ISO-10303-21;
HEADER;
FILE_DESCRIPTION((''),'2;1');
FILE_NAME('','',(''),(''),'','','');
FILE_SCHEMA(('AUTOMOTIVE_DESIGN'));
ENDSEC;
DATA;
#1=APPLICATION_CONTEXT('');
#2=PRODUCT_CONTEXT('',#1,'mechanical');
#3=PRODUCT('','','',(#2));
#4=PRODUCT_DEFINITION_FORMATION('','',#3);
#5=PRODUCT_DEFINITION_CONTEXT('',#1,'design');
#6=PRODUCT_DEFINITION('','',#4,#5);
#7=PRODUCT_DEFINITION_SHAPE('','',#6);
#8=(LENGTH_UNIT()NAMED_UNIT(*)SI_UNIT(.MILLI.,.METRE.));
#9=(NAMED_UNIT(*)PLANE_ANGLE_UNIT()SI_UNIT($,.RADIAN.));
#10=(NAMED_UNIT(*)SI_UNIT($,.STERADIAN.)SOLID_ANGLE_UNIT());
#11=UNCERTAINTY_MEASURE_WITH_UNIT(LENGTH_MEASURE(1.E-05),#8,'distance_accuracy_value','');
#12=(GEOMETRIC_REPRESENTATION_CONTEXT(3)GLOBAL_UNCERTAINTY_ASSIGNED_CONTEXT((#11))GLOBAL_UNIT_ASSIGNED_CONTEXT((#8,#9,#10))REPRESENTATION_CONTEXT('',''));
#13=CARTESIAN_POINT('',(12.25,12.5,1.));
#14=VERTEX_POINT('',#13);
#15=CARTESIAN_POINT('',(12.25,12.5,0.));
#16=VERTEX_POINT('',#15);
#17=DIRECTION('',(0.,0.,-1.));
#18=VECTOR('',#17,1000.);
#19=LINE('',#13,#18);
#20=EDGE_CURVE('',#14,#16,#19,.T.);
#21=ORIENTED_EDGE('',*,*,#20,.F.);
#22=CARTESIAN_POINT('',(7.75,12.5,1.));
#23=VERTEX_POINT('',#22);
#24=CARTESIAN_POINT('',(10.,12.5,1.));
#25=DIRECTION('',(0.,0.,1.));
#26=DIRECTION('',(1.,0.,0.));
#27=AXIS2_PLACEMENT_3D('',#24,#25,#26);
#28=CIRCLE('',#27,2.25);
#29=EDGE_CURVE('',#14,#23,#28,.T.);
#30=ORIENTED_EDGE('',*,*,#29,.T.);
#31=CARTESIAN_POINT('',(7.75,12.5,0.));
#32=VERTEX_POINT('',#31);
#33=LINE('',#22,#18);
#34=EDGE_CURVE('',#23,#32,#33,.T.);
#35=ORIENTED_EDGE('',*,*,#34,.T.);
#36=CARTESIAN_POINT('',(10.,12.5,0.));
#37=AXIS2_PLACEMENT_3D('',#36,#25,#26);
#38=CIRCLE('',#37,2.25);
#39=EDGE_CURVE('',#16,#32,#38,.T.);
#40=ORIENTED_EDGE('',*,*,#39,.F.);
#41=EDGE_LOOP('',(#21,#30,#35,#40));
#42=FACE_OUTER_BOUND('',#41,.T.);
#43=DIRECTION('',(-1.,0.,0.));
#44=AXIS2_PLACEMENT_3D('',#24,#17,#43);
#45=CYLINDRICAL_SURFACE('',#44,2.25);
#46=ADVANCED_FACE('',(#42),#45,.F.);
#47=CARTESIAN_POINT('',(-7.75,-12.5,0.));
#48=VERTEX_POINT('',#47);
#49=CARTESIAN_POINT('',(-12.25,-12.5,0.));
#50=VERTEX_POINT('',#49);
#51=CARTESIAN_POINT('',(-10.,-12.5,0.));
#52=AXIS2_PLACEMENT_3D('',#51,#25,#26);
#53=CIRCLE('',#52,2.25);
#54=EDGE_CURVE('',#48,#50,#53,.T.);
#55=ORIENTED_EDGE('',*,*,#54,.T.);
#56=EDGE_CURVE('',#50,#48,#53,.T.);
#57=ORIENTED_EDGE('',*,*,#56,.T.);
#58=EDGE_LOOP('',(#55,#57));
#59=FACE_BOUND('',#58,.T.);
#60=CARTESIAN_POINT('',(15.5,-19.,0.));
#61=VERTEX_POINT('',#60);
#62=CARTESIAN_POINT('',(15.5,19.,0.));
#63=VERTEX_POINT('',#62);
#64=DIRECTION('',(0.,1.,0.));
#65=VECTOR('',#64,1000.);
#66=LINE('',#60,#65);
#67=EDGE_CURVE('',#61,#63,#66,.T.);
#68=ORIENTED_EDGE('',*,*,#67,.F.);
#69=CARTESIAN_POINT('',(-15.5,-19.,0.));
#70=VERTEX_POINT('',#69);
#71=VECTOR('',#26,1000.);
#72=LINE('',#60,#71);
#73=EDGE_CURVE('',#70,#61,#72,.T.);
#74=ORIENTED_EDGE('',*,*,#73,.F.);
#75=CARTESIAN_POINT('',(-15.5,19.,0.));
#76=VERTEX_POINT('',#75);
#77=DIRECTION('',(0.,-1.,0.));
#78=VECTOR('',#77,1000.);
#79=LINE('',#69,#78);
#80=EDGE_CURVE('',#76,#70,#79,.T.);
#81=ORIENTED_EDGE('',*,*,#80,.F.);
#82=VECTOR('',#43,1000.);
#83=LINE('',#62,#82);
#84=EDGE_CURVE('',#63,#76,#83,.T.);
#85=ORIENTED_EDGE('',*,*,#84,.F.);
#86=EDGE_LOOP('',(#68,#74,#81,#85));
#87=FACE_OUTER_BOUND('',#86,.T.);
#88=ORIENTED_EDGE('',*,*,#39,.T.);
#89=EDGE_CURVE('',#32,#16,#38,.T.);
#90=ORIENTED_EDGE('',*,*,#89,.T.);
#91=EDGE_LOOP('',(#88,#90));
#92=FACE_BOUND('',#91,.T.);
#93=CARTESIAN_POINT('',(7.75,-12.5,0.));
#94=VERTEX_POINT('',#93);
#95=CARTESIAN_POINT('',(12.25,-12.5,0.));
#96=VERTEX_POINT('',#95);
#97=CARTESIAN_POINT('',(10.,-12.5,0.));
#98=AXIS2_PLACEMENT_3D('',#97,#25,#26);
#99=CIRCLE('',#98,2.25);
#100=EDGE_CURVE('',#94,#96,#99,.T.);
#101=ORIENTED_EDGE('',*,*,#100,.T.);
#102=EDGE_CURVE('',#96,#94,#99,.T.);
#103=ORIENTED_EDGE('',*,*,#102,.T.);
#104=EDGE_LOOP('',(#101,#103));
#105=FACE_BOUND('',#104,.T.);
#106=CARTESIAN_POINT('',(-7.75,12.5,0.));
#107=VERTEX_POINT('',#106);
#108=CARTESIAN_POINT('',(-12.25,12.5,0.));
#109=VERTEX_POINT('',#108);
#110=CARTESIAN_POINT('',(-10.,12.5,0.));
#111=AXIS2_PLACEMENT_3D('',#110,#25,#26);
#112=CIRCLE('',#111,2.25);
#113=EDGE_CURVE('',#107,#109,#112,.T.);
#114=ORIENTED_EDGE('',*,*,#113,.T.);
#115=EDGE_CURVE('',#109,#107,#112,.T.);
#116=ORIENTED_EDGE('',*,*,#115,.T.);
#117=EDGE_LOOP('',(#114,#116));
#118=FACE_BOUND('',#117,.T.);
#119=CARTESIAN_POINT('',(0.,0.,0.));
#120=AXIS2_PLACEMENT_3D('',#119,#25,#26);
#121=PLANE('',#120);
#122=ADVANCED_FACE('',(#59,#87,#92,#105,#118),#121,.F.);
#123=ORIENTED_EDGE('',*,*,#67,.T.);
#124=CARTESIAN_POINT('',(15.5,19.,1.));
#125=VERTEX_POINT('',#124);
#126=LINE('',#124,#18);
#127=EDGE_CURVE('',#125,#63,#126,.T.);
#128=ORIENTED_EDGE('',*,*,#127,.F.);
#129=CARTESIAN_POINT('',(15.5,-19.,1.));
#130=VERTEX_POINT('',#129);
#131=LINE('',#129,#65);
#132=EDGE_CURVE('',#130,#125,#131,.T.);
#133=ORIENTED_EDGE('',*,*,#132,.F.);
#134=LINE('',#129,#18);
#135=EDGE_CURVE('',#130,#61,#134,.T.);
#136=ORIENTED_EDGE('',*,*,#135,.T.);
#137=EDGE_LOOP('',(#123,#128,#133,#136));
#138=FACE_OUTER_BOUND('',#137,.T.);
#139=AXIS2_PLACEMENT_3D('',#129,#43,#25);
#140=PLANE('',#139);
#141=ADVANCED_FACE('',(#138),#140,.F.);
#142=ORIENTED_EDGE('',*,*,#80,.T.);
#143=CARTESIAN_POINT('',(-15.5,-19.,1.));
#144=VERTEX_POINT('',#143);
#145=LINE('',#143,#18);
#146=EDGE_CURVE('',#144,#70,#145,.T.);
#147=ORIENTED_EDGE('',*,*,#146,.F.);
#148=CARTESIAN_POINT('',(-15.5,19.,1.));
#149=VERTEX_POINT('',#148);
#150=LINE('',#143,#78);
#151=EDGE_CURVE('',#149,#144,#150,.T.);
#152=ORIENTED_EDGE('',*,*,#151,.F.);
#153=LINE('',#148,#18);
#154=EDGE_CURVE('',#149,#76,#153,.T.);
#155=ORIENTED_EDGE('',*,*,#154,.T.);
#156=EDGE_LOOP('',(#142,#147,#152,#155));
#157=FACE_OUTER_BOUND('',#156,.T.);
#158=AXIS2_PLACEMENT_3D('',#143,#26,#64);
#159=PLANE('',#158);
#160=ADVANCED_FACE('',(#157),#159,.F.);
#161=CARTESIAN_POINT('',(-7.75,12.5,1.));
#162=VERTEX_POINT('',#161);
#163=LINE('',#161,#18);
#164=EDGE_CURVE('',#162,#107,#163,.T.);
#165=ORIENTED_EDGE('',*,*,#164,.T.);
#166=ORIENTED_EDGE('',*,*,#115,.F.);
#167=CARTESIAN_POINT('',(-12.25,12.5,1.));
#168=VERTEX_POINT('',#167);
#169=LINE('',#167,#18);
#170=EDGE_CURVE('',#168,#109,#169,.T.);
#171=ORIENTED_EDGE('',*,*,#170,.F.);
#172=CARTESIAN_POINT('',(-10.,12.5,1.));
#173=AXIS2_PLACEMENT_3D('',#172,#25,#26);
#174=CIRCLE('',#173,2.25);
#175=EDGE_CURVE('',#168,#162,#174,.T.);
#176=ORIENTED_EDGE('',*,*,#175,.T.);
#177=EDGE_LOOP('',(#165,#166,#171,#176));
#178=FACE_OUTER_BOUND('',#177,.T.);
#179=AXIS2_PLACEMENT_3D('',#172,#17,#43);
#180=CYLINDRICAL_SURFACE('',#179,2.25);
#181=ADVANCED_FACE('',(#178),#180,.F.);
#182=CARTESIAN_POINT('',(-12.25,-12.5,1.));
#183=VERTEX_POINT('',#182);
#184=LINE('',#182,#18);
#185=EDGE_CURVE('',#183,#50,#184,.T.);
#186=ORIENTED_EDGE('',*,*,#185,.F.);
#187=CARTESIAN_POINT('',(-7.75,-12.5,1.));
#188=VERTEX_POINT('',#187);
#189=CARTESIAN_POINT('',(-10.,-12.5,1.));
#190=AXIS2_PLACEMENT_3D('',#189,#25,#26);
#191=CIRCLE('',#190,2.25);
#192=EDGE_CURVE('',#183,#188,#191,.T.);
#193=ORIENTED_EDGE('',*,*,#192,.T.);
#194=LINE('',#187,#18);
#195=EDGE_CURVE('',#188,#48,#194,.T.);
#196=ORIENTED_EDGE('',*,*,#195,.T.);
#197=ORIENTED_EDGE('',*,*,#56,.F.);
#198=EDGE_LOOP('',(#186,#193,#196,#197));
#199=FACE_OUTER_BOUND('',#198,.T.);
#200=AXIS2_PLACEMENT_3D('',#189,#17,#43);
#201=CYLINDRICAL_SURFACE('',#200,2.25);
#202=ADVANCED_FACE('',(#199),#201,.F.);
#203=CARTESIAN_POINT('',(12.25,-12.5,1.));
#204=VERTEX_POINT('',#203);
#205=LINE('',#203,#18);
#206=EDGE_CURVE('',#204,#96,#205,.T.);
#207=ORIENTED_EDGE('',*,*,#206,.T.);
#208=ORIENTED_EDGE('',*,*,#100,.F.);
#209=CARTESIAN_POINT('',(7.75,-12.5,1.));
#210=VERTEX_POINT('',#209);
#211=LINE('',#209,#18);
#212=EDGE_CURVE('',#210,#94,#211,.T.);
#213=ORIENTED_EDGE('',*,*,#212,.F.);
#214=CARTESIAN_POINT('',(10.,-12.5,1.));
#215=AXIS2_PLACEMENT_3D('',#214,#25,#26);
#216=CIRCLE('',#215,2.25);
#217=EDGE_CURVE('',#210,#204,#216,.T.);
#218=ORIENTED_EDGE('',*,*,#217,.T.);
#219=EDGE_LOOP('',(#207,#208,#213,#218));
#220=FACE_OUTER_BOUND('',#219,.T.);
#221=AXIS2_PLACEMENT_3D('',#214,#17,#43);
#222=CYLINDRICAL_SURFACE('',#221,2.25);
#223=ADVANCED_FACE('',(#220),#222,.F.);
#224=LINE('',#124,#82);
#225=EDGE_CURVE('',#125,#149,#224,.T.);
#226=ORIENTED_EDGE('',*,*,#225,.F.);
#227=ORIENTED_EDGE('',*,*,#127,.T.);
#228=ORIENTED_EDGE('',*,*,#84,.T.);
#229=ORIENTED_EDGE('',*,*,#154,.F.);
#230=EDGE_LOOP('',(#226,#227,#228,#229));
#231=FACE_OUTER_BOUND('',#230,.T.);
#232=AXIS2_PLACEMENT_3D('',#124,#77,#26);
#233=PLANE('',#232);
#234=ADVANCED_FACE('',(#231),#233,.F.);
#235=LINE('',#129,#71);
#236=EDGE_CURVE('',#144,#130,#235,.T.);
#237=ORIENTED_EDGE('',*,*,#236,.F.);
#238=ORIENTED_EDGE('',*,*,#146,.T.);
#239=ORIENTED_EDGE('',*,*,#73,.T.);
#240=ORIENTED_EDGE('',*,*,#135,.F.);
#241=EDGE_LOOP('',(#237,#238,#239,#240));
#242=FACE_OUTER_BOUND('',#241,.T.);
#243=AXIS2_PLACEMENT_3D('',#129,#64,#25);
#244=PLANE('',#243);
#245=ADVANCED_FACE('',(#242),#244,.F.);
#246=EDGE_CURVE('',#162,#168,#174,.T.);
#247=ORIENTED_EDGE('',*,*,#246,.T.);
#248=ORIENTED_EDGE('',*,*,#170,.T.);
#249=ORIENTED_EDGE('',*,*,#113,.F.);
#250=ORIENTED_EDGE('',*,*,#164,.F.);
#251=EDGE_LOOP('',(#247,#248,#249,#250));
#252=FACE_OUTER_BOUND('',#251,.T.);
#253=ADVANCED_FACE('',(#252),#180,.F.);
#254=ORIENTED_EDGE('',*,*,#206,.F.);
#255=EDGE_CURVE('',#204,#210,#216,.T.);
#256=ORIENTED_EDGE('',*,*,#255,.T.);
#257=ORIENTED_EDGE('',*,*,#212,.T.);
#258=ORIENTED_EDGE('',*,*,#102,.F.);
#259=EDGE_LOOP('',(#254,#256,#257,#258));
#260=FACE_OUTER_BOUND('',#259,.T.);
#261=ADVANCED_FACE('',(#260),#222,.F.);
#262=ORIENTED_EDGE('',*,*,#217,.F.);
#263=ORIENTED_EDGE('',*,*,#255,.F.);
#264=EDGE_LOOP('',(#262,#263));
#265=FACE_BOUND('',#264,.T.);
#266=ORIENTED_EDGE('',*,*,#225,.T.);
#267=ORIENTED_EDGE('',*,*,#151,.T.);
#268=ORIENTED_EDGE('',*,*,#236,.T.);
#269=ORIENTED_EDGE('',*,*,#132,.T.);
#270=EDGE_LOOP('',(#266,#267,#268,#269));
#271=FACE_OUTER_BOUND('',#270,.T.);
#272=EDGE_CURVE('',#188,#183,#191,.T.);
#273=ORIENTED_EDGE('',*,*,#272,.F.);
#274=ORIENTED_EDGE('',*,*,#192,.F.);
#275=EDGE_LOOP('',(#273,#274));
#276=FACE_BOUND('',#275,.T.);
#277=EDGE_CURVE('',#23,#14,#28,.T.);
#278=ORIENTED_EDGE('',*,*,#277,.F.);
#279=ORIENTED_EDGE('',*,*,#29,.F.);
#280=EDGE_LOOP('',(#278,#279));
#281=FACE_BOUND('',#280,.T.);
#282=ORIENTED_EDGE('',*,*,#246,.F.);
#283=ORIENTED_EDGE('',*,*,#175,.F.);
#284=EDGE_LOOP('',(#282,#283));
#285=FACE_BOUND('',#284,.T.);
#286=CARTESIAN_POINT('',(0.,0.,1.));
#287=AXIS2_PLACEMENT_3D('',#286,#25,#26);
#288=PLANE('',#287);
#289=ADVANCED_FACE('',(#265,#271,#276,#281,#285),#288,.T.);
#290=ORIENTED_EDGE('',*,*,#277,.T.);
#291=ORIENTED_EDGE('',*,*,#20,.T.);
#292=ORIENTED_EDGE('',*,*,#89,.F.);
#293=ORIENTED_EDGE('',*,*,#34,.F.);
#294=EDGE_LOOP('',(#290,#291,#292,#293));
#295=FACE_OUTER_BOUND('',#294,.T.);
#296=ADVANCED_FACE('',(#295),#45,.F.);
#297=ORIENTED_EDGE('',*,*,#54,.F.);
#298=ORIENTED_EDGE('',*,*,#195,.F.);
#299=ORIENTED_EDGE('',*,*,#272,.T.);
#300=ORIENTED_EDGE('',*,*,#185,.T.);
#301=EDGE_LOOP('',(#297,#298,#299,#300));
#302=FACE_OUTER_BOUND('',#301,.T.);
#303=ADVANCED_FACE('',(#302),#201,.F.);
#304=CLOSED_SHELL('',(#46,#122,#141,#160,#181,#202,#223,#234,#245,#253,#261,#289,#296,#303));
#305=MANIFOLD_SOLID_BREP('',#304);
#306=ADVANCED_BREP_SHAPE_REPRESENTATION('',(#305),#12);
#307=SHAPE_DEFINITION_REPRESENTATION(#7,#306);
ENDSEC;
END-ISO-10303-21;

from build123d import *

# Parameters (mm, degrees)
SKETCH_1_W      = 31
SKETCH_1_H      = 38
SKETCH_1_R      = 2.25
EXTRUDE_1_DEPTH = 1


with BuildPart() as part:
    # 草图1 → 凸台-拉伸1 (new body)
    with BuildSketch(Plane.XY):
        Rectangle(SKETCH_1_W, SKETCH_1_H)
        with Locations((-10, 12.5)):
            Circle(SKETCH_1_R, mode=Mode.SUBTRACT)
        with Locations((10, 12.5)):
            Circle(SKETCH_1_R, mode=Mode.SUBTRACT)
        with Locations((10, -12.5)):
            Circle(SKETCH_1_R, mode=Mode.SUBTRACT)
        with Locations((-10, -12.5)):
            Circle(SKETCH_1_R, mode=Mode.SUBTRACT)
    extrude(amount=EXTRUDE_1_DEPTH)


solid = part.part
